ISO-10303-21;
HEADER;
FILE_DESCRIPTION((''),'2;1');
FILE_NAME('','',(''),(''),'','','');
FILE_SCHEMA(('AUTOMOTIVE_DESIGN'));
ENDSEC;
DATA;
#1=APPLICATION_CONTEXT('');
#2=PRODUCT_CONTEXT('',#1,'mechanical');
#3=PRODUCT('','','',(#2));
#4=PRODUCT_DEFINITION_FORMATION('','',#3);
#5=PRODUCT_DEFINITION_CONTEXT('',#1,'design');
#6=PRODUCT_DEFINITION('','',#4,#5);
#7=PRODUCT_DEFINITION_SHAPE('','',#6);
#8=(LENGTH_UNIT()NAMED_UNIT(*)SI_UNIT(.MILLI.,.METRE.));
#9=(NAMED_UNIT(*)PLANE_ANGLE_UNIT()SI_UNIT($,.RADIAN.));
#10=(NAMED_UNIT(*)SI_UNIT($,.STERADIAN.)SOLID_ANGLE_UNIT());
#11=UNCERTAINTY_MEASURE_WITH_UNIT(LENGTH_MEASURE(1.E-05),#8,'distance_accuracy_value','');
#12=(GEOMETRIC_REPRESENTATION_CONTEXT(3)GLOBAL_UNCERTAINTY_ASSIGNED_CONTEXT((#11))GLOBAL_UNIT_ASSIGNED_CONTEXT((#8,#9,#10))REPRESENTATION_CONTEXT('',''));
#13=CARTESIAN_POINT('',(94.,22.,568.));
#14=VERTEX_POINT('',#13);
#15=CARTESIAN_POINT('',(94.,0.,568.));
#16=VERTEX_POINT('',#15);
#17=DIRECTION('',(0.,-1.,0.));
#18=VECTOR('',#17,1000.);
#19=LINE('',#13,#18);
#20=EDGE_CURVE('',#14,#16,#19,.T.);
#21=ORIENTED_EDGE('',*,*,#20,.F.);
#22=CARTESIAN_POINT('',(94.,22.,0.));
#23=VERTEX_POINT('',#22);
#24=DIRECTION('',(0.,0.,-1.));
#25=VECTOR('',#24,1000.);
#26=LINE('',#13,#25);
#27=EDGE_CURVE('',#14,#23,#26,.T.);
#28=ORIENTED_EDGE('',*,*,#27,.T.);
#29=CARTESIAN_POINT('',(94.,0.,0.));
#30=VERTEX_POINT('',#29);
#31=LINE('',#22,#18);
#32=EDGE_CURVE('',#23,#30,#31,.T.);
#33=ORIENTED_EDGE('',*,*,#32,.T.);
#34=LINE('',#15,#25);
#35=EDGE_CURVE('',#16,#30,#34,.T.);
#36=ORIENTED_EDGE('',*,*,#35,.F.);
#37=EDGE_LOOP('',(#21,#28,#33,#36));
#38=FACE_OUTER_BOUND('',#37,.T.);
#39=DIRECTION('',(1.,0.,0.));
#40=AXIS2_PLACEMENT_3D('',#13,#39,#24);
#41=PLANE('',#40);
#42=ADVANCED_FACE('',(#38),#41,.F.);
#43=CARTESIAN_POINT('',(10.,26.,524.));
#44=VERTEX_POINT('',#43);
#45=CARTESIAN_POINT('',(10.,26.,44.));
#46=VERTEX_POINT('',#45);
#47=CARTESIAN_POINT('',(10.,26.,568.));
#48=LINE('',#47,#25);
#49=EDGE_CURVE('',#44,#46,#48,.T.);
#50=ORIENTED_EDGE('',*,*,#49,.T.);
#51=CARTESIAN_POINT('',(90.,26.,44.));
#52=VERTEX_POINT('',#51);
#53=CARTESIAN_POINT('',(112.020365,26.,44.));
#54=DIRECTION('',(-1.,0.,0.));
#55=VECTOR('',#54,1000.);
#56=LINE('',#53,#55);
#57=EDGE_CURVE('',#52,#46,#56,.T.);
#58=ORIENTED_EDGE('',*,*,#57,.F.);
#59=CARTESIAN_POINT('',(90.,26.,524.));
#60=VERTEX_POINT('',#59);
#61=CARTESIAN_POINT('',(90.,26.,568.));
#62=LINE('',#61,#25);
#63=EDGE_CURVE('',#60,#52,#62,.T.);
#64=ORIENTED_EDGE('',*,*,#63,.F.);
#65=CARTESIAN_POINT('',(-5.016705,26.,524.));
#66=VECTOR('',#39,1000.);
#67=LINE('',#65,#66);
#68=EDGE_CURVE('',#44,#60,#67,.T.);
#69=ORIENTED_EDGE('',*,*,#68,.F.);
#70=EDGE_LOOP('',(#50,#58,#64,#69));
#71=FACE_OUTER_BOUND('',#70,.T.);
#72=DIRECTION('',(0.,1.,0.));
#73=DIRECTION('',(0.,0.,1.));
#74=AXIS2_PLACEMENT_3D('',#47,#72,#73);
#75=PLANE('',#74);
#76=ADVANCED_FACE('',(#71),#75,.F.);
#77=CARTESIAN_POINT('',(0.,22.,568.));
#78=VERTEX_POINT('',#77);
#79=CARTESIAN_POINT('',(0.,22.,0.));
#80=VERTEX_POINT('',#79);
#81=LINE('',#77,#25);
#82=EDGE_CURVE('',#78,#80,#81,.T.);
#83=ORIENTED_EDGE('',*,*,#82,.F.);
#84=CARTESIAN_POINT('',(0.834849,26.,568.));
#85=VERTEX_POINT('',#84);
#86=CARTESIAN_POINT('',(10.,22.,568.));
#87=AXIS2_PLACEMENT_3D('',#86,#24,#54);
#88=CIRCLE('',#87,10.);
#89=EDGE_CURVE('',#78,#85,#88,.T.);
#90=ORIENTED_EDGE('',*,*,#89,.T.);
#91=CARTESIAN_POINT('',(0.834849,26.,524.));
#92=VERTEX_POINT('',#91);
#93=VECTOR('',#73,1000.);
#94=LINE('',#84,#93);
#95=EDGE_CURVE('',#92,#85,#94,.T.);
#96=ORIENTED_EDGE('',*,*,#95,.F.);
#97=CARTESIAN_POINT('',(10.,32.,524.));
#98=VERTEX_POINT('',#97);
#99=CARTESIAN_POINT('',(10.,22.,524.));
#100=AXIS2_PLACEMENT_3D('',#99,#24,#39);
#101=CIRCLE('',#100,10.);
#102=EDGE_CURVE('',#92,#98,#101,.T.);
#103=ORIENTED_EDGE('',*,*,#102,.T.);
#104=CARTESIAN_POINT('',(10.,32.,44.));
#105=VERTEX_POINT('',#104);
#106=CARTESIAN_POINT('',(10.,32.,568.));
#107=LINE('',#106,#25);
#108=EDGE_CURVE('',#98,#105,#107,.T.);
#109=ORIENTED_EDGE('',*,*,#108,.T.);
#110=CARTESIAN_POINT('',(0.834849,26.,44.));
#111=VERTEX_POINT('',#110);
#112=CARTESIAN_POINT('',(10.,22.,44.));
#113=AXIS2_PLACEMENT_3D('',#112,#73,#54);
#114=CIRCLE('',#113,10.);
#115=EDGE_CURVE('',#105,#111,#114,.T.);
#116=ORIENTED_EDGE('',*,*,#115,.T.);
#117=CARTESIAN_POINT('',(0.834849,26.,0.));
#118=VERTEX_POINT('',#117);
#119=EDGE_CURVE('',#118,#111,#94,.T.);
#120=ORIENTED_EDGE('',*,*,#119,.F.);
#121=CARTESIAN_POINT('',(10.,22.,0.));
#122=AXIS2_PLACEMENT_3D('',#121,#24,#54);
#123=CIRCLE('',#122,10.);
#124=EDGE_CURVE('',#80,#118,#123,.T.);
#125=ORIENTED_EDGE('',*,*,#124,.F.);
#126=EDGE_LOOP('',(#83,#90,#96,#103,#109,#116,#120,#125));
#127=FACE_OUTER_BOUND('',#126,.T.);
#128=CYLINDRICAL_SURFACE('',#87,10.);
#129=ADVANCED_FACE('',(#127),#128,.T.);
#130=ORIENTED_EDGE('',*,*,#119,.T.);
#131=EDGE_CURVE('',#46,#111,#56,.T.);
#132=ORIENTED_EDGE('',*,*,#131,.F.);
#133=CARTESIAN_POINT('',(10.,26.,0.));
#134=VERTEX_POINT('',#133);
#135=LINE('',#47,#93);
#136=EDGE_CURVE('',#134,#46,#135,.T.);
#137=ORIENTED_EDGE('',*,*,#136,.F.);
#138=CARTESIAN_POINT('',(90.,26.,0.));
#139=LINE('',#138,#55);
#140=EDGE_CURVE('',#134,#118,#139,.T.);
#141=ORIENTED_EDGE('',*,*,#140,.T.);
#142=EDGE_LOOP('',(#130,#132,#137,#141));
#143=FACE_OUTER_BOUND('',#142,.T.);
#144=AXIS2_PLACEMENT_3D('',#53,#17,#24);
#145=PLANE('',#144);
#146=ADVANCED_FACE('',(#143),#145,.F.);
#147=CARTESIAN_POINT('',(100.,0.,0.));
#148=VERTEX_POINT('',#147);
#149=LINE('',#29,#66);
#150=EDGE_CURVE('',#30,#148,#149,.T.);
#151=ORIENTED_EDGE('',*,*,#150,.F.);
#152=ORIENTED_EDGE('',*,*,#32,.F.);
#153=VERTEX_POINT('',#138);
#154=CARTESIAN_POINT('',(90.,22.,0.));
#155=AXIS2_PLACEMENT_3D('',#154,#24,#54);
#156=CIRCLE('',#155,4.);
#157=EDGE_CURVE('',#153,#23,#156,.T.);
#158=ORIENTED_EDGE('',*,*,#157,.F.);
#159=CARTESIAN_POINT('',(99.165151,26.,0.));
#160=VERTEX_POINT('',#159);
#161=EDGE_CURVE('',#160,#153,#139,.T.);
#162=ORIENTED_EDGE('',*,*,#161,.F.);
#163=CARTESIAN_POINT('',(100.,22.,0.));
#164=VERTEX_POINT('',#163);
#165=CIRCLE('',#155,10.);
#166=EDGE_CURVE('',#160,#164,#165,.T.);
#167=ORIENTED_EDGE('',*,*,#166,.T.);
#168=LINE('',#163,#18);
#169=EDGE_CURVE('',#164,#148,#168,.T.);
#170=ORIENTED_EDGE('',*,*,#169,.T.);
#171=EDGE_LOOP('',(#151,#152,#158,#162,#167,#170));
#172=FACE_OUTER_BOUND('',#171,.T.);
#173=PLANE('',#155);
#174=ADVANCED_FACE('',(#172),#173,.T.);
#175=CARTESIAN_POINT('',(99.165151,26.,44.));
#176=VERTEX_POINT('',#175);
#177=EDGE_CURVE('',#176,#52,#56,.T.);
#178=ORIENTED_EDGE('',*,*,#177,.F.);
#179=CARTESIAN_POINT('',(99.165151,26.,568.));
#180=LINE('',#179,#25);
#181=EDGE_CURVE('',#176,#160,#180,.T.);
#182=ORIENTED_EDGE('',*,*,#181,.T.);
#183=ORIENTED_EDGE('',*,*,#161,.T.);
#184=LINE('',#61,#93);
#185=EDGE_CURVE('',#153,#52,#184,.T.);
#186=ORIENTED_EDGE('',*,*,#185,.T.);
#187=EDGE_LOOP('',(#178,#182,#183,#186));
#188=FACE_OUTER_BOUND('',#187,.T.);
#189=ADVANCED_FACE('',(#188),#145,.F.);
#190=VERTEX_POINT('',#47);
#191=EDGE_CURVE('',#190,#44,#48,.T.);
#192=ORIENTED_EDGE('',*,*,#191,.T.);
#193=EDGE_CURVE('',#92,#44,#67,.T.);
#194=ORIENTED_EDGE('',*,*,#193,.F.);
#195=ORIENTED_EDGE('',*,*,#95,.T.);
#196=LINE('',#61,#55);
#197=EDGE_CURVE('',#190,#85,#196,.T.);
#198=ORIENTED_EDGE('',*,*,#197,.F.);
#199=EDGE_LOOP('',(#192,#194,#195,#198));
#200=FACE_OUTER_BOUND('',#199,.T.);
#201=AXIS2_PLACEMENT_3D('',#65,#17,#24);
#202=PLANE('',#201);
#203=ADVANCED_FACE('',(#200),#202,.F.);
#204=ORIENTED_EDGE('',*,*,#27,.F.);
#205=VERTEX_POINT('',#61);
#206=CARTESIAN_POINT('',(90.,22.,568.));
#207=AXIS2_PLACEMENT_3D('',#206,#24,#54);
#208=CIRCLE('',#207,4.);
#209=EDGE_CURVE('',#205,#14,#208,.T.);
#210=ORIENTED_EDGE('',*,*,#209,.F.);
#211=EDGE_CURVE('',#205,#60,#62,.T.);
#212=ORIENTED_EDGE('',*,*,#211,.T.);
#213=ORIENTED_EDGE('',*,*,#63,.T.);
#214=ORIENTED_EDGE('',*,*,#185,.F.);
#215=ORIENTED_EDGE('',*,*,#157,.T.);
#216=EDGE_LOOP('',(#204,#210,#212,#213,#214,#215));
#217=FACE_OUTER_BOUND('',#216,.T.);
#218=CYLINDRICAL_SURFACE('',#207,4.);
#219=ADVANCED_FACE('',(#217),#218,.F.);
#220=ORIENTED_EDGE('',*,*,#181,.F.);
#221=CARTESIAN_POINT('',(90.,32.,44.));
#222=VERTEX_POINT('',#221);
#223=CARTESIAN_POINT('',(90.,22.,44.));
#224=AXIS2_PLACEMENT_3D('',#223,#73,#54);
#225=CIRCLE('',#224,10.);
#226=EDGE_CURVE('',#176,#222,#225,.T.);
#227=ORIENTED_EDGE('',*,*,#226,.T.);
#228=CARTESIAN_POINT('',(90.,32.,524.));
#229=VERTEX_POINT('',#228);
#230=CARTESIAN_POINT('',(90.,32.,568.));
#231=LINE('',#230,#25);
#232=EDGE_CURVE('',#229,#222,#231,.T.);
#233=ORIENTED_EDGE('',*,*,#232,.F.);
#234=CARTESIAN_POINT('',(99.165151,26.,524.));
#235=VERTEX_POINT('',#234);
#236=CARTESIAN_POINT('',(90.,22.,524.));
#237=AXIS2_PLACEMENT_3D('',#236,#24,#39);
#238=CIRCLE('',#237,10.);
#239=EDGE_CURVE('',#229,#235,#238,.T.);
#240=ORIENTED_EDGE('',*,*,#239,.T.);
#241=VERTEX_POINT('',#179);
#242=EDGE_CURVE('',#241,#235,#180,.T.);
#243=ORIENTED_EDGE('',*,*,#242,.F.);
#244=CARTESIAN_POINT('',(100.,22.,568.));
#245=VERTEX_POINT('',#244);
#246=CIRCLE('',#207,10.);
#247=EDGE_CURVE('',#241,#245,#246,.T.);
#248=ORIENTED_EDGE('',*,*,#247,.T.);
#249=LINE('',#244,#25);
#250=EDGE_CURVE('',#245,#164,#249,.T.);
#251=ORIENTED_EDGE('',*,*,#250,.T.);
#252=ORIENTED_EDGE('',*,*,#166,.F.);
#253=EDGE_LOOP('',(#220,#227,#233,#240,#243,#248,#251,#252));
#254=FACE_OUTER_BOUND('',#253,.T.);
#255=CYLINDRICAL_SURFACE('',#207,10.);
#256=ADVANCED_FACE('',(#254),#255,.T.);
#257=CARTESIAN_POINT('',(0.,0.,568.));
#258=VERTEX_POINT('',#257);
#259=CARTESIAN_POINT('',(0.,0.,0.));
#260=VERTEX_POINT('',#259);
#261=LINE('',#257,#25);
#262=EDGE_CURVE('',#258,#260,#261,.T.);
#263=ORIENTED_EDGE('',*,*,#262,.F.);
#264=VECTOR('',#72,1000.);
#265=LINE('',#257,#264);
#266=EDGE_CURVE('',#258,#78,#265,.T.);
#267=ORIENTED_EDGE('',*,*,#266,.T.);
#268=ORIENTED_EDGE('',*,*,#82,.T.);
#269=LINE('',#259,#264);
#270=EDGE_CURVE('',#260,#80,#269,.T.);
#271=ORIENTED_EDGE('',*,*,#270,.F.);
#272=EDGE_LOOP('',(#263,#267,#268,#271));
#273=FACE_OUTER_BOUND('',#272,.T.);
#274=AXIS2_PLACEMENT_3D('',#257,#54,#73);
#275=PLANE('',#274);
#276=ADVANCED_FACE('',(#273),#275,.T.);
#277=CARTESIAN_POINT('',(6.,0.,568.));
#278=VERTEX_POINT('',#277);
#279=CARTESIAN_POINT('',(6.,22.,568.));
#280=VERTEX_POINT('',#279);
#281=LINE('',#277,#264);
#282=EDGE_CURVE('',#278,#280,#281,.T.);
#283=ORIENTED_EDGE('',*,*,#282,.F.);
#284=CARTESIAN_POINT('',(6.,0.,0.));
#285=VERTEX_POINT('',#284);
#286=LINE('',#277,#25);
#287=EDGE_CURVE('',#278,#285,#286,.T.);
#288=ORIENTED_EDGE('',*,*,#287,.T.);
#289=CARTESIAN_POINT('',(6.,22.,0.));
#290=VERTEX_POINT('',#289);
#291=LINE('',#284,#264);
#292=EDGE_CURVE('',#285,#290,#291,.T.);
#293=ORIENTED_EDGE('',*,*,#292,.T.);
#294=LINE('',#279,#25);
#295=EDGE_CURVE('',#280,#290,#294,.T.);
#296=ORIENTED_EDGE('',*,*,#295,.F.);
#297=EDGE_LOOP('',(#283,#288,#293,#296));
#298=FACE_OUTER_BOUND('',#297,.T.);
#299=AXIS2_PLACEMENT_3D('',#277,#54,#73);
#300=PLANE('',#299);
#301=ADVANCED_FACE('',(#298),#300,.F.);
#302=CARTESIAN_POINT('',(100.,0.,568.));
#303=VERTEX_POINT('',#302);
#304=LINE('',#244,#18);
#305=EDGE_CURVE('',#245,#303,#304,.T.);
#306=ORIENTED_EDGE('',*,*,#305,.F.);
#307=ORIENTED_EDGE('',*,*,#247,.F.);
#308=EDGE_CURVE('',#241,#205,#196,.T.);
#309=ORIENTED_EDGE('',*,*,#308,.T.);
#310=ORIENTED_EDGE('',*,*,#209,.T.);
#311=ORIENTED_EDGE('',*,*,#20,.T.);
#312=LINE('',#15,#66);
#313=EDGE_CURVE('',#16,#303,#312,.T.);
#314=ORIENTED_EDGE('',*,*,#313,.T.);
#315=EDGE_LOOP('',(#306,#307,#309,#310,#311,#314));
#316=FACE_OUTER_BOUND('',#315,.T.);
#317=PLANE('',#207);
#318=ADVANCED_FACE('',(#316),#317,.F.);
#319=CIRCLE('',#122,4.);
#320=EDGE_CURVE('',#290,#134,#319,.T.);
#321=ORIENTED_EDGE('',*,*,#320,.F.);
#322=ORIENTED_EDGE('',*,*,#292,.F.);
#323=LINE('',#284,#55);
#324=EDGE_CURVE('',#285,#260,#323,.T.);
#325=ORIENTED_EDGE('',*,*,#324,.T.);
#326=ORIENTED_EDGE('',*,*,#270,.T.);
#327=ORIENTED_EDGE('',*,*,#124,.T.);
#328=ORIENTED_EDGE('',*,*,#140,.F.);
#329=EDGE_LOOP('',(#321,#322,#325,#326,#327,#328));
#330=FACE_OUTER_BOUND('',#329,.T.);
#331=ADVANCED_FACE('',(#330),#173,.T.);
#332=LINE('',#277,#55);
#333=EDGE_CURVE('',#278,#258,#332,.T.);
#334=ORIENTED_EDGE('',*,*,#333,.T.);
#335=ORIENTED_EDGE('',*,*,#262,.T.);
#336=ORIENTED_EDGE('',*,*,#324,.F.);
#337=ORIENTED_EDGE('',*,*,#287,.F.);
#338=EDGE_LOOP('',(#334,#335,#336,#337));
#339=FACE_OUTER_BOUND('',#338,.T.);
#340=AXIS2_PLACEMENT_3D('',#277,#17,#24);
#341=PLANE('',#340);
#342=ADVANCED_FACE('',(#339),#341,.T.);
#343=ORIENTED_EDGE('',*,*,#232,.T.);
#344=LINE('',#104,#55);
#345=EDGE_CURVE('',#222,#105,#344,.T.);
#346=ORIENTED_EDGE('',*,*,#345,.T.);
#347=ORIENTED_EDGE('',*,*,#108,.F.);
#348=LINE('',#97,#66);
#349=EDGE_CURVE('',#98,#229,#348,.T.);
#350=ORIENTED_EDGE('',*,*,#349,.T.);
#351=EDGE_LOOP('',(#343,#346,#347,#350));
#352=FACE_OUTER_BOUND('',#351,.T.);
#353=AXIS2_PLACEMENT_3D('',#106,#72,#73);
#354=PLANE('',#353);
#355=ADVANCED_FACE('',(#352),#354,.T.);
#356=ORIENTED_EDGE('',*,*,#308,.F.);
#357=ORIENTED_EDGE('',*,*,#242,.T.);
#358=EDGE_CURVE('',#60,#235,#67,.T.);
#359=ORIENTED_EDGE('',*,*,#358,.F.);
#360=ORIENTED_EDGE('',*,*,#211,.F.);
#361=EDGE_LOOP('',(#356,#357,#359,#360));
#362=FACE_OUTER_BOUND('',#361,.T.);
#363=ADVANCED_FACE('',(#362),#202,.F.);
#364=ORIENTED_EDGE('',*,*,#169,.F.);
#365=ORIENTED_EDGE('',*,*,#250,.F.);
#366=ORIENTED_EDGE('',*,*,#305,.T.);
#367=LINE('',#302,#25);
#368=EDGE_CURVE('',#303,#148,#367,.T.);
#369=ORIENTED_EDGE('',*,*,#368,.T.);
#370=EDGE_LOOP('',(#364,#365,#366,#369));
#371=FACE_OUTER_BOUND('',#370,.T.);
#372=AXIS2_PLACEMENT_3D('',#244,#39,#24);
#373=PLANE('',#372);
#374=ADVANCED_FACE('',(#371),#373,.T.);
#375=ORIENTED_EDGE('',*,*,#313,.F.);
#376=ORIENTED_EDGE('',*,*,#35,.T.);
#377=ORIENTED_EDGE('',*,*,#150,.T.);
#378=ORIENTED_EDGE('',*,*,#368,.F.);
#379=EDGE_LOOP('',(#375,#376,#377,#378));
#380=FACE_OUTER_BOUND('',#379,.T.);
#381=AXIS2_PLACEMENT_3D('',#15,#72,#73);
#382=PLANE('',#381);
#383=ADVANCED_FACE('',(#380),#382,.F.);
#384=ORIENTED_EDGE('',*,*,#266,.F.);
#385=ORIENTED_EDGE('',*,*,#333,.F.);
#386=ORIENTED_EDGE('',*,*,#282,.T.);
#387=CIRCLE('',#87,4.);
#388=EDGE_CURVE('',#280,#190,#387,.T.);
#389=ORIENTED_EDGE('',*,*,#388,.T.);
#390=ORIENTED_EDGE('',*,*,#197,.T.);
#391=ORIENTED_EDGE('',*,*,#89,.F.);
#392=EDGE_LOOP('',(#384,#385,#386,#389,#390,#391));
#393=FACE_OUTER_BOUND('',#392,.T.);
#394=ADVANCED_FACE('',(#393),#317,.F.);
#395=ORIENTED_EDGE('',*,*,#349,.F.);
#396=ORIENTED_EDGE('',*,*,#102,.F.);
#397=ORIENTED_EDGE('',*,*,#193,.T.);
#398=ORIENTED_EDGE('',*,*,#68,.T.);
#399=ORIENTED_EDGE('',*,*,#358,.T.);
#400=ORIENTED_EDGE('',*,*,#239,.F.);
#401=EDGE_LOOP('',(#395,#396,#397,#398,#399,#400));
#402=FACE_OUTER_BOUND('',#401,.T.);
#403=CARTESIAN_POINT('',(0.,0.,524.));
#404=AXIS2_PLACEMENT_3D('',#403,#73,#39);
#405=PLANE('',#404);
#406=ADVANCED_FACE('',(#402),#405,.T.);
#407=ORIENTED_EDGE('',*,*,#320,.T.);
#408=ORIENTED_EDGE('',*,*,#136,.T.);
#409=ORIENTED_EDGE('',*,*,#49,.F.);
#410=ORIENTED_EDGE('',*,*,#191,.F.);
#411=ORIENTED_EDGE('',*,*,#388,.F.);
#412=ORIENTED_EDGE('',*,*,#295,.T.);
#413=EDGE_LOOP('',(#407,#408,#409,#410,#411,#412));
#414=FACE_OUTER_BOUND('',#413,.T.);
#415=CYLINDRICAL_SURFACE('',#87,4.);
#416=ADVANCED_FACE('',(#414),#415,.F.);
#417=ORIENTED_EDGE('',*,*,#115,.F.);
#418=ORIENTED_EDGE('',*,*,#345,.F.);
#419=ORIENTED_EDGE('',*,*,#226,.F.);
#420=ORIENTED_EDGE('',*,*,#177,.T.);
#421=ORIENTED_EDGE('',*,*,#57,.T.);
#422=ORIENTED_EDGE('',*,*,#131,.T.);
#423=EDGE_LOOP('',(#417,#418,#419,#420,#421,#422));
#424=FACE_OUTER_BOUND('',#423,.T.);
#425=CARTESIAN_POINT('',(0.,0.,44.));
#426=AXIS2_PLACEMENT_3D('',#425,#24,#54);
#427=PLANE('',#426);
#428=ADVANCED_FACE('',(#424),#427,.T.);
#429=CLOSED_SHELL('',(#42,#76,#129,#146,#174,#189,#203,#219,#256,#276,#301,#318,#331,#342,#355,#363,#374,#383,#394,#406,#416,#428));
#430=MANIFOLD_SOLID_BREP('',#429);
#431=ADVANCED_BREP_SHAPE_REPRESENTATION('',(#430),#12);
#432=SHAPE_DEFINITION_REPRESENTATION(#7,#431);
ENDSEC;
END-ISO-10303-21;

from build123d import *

# Parameters (mm, degrees)
BOSS_EXTRUDE1_DEPTH = 568
CUT_EXTRUDE1_DEPTH  = 44
CUT_EXTRUDE2_DEPTH  = 44


with BuildPart() as part:
    # Sketch1 → Boss-Extrude1 (new body)
    with BuildSketch(Plane.XY):
        with BuildLine():
            Line((0, 0), (0, 22))
            ThreePointArc((0, 22), (2.928932188, 29.071067812), (10, 32))
            Line((10, 32), (90, 32))
            ThreePointArc((90, 32), (97.071067812, 29.071067812), (100, 22))
            Line((100, 22), (100, 0))
            Line((100, 0), (94, 0))
            Line((94, 0), (94, 22))
            ThreePointArc((94, 22), (92.828427125, 24.828427125), (90, 26))
            Line((90, 26), (10, 26))
            ThreePointArc((10, 26), (7.171572875, 24.828427125), (6, 22))
            Line((6, 22), (6, 0))
            Line((6, 0), (0, 0))
        make_face()
    extrude(amount=BOSS_EXTRUDE1_DEPTH)

    # Sketch2 → Cut-Extrude1 (cut)
    with BuildSketch(Plane.XY.offset(568)):
        Polygon((-5.016704774, 26), (110.589606684, 26), (113.542758838, 46.117705453), (4.096772107, 46.117705453), (-12.020365044, 28.61582492), align=None)
    extrude(amount=-CUT_EXTRUDE1_DEPTH, mode=Mode.SUBTRACT)

    # Sketch3 → Cut-Extrude2 (cut)
    with BuildSketch(Plane(origin=(0, 0, 0), x_dir=(-1, 0, 0), z_dir=(0, 0, -1))):
        Polygon((-112.020365044, 26), (27.466483662, 26), (17.252014884, 45.492114728), (-47.890463774, 56.039795858), (-51.518866083, 56.039795858), (-99.243616331, 54.20535901), align=None)
    extrude(amount=-CUT_EXTRUDE2_DEPTH, mode=Mode.SUBTRACT)


solid = part.part
